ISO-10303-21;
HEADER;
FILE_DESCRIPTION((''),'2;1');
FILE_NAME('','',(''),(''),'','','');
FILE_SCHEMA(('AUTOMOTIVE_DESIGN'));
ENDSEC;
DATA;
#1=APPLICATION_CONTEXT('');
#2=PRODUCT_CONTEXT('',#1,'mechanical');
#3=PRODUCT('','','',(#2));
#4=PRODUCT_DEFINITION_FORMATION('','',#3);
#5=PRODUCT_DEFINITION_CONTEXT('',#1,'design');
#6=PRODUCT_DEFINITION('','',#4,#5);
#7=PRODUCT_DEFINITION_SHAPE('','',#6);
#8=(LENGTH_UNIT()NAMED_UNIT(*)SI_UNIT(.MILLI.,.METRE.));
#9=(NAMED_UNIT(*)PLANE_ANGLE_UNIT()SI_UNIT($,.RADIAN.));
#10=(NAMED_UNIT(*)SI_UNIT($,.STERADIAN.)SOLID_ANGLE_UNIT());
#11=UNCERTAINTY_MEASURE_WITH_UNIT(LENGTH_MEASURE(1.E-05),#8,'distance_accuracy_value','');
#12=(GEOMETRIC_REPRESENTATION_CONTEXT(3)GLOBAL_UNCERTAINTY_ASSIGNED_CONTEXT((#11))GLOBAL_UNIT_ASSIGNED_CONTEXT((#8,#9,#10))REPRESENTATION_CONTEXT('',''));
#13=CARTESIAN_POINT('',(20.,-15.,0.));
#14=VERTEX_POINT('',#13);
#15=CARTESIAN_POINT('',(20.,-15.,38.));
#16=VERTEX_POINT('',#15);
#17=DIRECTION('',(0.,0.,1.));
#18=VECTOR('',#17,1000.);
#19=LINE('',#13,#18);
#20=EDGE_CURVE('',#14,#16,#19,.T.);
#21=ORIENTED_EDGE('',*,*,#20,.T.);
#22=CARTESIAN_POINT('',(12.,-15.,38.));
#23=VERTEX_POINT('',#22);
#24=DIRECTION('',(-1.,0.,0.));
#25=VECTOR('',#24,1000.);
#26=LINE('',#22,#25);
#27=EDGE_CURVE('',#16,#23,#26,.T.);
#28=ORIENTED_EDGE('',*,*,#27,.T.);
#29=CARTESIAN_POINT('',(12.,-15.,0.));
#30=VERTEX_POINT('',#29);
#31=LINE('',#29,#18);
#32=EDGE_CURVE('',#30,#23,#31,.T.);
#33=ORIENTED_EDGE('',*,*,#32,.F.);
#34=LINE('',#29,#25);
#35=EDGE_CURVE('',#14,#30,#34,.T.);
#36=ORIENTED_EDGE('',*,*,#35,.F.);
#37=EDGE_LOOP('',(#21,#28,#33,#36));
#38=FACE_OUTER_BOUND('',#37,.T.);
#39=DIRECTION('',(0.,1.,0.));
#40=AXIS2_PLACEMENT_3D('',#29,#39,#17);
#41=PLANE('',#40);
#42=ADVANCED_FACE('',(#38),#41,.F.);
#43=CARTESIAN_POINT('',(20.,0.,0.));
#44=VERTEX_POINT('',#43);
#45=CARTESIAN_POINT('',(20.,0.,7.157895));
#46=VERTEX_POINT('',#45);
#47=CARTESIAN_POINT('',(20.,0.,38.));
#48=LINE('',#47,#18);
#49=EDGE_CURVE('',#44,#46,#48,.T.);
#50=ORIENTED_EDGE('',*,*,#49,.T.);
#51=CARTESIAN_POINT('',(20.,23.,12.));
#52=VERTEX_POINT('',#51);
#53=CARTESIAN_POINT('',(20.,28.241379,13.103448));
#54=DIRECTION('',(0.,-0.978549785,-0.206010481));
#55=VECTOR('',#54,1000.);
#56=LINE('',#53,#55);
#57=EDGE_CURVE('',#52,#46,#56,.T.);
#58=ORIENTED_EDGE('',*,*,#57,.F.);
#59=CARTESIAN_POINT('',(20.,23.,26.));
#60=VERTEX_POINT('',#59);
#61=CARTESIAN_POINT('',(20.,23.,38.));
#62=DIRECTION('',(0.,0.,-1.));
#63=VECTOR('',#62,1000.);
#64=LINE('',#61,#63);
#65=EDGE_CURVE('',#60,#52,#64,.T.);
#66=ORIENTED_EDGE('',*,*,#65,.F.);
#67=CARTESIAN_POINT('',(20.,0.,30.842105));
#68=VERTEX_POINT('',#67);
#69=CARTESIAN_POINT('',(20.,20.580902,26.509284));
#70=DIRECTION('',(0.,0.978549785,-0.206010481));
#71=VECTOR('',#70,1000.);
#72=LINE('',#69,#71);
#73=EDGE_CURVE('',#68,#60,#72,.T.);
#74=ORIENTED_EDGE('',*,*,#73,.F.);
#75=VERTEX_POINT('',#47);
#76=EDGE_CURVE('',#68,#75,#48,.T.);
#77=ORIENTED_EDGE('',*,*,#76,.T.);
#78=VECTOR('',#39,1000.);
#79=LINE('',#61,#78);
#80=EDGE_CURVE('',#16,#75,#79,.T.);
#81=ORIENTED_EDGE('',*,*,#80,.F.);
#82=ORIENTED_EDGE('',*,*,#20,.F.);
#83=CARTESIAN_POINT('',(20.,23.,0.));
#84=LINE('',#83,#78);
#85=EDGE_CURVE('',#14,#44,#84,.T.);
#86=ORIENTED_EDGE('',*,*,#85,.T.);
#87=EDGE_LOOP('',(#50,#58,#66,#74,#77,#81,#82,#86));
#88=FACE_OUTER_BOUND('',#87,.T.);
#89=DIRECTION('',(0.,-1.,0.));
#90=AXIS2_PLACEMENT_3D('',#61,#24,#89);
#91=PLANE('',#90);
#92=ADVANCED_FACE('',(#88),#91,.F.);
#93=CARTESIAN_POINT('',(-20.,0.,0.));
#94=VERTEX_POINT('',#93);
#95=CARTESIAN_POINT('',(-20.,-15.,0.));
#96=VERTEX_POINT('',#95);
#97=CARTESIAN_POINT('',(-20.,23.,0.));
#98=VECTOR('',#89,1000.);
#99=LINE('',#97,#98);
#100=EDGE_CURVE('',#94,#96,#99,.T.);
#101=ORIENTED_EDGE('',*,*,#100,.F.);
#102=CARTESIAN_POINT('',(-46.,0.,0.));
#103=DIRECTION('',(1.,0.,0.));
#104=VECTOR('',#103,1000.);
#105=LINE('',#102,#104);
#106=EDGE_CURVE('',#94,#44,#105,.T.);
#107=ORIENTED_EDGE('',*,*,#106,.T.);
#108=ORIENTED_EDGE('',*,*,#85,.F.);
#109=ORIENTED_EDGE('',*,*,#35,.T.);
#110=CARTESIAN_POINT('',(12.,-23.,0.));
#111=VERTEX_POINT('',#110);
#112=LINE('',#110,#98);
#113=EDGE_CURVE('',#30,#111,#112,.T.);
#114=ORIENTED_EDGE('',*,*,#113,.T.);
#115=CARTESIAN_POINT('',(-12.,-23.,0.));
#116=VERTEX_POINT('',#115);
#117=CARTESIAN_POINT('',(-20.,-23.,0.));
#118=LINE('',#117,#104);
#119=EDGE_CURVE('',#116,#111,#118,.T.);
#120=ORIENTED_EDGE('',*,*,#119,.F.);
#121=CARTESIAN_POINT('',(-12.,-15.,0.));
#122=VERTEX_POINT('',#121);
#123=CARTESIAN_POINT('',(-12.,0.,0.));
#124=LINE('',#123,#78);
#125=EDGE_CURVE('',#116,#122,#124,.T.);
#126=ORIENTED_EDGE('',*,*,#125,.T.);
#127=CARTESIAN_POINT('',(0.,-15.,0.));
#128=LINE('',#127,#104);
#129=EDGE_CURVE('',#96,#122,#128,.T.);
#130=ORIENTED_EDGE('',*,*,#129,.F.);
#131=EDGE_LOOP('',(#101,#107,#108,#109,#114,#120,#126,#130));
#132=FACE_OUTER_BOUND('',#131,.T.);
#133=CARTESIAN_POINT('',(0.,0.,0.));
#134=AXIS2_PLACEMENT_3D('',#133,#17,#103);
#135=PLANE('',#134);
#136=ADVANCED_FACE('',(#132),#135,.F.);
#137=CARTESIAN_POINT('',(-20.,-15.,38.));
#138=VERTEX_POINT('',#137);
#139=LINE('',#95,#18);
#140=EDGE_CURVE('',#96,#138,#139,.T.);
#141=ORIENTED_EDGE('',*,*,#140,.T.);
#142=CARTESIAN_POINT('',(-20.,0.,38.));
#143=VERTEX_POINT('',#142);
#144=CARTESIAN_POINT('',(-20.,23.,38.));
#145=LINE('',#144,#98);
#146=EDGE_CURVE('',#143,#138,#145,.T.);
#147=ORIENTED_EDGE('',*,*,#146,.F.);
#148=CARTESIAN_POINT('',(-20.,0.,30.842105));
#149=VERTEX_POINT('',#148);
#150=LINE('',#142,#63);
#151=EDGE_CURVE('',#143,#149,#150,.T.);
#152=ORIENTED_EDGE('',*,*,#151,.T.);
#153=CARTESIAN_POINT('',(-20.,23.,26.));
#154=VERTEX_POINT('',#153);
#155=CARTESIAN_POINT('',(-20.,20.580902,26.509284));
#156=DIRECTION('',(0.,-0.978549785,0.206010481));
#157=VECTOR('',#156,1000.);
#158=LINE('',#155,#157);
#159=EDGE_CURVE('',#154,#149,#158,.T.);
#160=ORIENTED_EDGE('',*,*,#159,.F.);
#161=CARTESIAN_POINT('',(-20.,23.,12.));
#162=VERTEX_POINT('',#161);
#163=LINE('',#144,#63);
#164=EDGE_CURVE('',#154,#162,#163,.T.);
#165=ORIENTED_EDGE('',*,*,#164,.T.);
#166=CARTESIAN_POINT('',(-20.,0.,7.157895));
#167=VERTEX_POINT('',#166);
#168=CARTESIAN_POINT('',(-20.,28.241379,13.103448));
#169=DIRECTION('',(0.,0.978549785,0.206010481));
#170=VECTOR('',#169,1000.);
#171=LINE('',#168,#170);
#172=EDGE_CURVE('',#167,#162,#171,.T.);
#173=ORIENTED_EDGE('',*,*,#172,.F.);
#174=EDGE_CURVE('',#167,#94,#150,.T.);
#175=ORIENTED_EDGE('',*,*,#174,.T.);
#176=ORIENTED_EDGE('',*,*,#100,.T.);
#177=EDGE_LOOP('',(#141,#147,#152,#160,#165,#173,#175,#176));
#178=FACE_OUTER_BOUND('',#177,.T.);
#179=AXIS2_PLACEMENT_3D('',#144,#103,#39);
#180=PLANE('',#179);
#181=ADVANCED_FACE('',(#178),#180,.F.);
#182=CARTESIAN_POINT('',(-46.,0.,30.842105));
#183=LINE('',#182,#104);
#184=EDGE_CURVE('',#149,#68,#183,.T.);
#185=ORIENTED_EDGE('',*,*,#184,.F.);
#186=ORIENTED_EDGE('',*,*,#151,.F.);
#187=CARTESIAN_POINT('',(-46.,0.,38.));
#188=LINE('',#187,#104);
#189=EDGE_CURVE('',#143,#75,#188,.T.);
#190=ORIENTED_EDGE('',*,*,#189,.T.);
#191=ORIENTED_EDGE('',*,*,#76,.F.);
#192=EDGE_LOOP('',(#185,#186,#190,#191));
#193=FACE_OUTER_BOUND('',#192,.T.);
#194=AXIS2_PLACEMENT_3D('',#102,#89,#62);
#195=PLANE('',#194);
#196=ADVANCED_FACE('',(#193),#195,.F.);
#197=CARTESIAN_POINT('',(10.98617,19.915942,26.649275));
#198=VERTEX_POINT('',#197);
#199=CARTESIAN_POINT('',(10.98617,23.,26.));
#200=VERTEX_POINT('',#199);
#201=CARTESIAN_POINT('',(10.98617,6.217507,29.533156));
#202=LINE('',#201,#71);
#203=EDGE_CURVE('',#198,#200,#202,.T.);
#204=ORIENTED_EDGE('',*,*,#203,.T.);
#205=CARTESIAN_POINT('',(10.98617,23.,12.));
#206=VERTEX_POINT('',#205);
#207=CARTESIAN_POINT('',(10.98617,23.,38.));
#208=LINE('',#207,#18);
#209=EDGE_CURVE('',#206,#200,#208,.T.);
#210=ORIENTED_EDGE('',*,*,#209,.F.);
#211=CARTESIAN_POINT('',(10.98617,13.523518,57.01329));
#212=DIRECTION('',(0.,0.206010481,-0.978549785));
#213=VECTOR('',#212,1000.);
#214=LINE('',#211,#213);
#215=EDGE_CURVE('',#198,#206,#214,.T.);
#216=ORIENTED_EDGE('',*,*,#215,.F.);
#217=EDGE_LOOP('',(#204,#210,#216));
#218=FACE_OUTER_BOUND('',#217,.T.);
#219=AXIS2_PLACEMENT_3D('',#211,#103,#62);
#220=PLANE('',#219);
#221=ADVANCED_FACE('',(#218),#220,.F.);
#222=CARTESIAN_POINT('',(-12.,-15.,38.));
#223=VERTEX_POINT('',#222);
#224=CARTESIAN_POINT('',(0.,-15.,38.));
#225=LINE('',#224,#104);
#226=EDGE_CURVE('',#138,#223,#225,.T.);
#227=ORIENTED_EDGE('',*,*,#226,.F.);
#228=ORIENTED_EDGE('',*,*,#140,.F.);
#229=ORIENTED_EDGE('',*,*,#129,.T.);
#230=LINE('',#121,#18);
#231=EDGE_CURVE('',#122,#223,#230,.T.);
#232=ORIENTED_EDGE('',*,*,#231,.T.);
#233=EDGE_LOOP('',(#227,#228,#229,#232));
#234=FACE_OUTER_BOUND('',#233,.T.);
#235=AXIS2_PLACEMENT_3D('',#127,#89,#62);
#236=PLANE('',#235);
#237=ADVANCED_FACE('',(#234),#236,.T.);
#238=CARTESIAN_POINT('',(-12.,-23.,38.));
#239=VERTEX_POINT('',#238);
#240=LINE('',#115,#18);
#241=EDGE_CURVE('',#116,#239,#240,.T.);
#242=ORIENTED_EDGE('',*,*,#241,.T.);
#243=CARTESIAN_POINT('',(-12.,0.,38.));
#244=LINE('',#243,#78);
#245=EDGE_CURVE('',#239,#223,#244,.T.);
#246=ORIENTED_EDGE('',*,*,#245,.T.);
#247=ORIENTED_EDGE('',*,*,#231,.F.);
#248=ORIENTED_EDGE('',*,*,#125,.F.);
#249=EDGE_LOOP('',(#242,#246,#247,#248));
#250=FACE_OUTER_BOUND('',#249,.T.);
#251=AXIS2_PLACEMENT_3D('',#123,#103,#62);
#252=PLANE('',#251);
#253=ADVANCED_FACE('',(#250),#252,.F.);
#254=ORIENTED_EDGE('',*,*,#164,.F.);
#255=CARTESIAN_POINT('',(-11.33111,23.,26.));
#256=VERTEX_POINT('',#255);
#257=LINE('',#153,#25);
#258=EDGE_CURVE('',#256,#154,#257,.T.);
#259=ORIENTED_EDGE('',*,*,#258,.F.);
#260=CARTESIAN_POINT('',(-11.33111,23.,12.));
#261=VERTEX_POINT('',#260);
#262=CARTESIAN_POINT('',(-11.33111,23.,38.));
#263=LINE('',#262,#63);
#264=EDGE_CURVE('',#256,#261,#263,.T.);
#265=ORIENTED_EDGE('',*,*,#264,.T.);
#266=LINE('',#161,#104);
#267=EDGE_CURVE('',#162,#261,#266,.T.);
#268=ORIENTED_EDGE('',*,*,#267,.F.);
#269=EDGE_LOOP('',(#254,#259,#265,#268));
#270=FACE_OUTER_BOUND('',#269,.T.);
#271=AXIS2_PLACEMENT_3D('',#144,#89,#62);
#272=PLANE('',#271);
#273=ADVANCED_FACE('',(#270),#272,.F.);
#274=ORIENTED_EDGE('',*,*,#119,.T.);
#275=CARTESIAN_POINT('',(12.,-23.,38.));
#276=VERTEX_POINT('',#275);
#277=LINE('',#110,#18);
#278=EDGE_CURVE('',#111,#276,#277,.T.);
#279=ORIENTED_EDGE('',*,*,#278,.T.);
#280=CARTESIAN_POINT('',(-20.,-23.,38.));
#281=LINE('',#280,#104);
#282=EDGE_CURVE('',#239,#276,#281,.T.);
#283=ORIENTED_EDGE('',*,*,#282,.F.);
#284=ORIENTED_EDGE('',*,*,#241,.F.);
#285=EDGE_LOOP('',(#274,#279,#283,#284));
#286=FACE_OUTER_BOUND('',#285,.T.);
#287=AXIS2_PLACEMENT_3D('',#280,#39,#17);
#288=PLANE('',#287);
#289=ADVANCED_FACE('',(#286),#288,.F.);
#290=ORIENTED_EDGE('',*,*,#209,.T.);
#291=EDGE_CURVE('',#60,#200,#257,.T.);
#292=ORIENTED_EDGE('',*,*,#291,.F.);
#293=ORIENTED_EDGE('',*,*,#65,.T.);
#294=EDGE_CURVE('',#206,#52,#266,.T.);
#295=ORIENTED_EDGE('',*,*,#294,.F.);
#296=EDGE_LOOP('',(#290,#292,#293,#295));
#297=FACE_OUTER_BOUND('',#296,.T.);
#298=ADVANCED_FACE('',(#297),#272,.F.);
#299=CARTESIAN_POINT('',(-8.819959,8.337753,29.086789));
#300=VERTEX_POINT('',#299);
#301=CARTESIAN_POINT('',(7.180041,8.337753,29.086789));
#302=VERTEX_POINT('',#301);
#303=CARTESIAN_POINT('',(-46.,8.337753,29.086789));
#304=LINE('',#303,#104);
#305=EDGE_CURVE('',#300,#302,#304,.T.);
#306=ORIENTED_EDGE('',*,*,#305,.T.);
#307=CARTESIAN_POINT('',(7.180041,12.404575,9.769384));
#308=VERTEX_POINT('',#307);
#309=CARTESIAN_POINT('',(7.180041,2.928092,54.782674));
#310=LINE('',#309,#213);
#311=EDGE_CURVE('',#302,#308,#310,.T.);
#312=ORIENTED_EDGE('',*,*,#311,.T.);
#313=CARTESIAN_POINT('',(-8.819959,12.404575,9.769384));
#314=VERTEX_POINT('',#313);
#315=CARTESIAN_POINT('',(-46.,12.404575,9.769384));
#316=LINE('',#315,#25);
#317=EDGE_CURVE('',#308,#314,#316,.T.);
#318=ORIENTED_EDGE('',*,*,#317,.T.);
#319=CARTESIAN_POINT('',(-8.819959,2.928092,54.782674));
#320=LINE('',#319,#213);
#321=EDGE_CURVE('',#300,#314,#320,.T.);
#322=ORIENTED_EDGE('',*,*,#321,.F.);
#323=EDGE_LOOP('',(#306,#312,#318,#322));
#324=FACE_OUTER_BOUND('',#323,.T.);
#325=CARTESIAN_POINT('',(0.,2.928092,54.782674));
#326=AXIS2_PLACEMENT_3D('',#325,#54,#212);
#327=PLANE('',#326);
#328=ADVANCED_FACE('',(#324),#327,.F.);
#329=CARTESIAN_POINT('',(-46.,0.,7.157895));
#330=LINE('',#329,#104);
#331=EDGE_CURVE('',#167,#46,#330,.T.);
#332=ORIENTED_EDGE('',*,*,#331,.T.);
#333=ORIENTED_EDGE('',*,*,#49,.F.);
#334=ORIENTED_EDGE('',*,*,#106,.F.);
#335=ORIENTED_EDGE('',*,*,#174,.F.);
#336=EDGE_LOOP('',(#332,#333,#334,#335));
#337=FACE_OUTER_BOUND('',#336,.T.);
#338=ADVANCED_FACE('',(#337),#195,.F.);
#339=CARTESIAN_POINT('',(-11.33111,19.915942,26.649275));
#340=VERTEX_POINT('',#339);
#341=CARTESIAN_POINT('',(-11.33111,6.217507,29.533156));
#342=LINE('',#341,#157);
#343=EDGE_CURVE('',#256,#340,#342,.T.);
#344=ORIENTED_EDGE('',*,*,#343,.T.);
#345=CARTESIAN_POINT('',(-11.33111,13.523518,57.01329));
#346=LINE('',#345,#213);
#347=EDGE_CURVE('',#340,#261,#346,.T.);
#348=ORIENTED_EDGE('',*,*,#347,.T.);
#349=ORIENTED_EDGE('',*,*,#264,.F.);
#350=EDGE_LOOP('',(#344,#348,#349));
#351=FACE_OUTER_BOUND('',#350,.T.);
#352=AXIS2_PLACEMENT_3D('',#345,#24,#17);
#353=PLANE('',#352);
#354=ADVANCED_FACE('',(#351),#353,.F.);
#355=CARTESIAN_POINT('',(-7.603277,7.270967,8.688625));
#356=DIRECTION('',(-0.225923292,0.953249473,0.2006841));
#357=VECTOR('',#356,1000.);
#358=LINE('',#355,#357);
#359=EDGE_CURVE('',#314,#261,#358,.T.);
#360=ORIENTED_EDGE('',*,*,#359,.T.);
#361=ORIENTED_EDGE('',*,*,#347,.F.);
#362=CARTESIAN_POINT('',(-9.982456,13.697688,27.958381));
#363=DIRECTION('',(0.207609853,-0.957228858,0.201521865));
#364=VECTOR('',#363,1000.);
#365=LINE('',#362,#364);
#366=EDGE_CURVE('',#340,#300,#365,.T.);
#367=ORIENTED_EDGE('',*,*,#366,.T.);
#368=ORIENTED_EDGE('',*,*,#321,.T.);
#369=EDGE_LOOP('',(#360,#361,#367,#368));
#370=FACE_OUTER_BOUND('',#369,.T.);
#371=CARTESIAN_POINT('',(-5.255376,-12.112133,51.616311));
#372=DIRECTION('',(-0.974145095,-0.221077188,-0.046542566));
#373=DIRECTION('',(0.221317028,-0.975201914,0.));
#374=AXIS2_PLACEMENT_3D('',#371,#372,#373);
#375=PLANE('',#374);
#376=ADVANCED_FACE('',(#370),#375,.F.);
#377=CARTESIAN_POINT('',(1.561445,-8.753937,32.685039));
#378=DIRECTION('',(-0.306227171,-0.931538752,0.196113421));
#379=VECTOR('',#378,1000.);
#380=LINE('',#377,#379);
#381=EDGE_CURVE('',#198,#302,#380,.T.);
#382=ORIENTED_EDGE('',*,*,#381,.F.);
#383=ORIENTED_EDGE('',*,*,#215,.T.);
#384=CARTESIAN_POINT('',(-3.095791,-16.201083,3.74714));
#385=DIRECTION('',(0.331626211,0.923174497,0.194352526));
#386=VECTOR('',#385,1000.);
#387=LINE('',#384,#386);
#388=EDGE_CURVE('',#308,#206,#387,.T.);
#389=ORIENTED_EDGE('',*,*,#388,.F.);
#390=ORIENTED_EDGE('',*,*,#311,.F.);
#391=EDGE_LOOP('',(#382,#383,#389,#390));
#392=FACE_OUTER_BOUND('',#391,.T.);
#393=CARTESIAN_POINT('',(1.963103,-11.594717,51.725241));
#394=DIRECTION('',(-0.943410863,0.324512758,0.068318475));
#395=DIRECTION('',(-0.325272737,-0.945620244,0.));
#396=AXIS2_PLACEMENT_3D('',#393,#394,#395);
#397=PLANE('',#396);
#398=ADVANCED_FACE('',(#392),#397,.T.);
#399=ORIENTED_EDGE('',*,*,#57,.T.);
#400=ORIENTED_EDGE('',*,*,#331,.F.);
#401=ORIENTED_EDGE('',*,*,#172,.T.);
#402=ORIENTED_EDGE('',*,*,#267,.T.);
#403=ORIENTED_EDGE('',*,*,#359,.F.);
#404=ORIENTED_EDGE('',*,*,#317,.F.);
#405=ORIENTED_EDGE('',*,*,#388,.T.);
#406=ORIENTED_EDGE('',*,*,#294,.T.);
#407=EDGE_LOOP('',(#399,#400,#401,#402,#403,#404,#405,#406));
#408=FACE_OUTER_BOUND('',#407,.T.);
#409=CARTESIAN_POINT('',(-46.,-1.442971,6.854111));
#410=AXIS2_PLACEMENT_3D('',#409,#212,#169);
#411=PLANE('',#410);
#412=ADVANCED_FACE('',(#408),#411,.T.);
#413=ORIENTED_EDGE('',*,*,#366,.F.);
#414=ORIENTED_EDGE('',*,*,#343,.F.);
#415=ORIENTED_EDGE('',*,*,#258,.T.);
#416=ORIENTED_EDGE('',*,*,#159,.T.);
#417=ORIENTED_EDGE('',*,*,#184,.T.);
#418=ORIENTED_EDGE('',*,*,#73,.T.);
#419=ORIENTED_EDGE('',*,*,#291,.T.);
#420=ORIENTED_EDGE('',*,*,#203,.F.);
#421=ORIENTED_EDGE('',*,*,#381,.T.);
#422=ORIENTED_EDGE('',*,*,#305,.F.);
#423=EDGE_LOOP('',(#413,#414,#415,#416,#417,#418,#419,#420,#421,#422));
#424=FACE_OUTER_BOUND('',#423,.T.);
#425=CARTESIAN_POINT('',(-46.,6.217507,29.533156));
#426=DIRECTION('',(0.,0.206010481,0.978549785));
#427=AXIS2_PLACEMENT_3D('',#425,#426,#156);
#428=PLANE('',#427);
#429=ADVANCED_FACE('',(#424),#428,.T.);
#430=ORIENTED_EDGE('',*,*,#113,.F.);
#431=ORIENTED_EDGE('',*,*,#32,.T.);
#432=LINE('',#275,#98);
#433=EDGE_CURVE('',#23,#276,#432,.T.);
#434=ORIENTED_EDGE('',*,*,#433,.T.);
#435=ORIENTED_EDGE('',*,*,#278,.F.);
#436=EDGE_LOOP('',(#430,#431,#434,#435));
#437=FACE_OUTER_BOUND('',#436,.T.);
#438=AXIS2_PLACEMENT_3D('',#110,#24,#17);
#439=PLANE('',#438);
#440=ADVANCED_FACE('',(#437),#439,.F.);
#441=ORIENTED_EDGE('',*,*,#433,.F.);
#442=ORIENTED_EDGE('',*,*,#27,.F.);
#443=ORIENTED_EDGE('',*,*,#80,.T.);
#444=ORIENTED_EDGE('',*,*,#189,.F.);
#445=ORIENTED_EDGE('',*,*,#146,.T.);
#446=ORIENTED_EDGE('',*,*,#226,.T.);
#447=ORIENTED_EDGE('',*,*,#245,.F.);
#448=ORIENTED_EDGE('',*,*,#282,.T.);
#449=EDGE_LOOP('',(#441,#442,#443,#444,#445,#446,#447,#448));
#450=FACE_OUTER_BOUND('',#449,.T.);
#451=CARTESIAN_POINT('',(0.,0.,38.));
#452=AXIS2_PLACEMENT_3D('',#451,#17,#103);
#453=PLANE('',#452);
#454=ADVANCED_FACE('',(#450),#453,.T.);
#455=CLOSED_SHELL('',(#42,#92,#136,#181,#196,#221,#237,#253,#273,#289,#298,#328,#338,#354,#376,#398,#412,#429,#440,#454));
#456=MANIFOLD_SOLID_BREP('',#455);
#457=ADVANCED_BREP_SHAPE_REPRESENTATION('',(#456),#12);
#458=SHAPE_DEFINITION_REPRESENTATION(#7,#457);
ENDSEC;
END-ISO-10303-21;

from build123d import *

# Parameters (mm, degrees)
BASE_PROFILE_SKETCH_W  = 40
BASE_PROFILE_SKETCH_H  = 46
BASE_BLOCK_DEPTH       = 38
BOTTOM_STEP_SKETCH_W   = 8
BOTTOM_STEP_SKETCH_H   = 8
BOTTOM_STEP_CUT_DEPTH  = 49.713447835
CORNER_NOTCH_SKETCH_W  = 8
CORNER_NOTCH_SKETCH_H  = 8
CORNER_NOTCH_8X8_DEPTH = 49.713447835
V_GROOVE_CUT_DEPTH     = 46
SLOT_CUT_8X8_DEPTH     = 46
SIDE_TRIM_SKETCH_W     = 22.317279544
SIDE_TRIM_SKETCH_H     = 4.669832792
SIDE_TRIM_CUT_DEPTH    = 46


with BuildPart() as part:
    # Base Profile Sketch → Base Block (new body)
    with BuildSketch(Plane.XY):
        Rectangle(BASE_PROFILE_SKETCH_W, BASE_PROFILE_SKETCH_H)
    extrude(amount=BASE_BLOCK_DEPTH)

    # Bottom Step Sketch → Bottom Step Cut (cut, through all)
    with BuildSketch(Plane.XY.offset(38)):
        with Locations((-16, -19)):
            Rectangle(BOTTOM_STEP_SKETCH_W, BOTTOM_STEP_SKETCH_H)
    extrude(amount=-BOTTOM_STEP_CUT_DEPTH, mode=Mode.SUBTRACT)

    # Corner Notch Sketch → Corner Notch 8x8 (cut, through all)
    with BuildSketch(Plane.XY.offset(38)):
        with Locations((16, -19)):
            Rectangle(CORNER_NOTCH_SKETCH_W, CORNER_NOTCH_SKETCH_H)
    extrude(amount=-CORNER_NOTCH_8X8_DEPTH, mode=Mode.SUBTRACT)

    # V-Groove Profile Sketch → V-Groove Cut (cut, symmetric)
    with BuildSketch(Plane(origin=(0, 0, 0), x_dir=(0, 0, -1), z_dir=(1, 0, 0))):
        Polygon((-38, 0), (-30.842105263, 0), (-26, 23), (-38, 23), align=None)
        Polygon((-12, 23), (-7.157894737, 0), (0, 0), (0, 23), align=None)
    extrude(amount=V_GROOVE_CUT_DEPTH, both=True, mode=Mode.SUBTRACT)

    # Slot Sketch → Slot Cut 8x8 (cut, symmetric)
    with BuildSketch(Plane(origin=(0, -1.442970822, 6.854111406), x_dir=(-1, 0, 0), z_dir=(0, 0.206010481049842, -0.9785497849867492))):
        Polygon((-7.180041029, 14.15108932), (0.819958971, 14.15108932), (8.819958971, 14.15108932), (11.331109989, 24.978770827), (-10.986169555, 24.978770827), align=None)
    extrude(amount=SLOT_CUT_8X8_DEPTH, both=True, mode=Mode.SUBTRACT)

    # Side Trim Sketch → Side Trim Cut (cut, symmetric)
    with BuildSketch(Plane(origin=(0, -1.442970822, 6.854111406), x_dir=(-1, 0, 0), z_dir=(0, 0.206010481049842, -0.9785497849867492))):
        with Locations((0.172470217, 27.313687223)):
            Rectangle(SIDE_TRIM_SKETCH_W, SIDE_TRIM_SKETCH_H)
    extrude(amount=SIDE_TRIM_CUT_DEPTH, both=True, mode=Mode.SUBTRACT)


solid = part.part
